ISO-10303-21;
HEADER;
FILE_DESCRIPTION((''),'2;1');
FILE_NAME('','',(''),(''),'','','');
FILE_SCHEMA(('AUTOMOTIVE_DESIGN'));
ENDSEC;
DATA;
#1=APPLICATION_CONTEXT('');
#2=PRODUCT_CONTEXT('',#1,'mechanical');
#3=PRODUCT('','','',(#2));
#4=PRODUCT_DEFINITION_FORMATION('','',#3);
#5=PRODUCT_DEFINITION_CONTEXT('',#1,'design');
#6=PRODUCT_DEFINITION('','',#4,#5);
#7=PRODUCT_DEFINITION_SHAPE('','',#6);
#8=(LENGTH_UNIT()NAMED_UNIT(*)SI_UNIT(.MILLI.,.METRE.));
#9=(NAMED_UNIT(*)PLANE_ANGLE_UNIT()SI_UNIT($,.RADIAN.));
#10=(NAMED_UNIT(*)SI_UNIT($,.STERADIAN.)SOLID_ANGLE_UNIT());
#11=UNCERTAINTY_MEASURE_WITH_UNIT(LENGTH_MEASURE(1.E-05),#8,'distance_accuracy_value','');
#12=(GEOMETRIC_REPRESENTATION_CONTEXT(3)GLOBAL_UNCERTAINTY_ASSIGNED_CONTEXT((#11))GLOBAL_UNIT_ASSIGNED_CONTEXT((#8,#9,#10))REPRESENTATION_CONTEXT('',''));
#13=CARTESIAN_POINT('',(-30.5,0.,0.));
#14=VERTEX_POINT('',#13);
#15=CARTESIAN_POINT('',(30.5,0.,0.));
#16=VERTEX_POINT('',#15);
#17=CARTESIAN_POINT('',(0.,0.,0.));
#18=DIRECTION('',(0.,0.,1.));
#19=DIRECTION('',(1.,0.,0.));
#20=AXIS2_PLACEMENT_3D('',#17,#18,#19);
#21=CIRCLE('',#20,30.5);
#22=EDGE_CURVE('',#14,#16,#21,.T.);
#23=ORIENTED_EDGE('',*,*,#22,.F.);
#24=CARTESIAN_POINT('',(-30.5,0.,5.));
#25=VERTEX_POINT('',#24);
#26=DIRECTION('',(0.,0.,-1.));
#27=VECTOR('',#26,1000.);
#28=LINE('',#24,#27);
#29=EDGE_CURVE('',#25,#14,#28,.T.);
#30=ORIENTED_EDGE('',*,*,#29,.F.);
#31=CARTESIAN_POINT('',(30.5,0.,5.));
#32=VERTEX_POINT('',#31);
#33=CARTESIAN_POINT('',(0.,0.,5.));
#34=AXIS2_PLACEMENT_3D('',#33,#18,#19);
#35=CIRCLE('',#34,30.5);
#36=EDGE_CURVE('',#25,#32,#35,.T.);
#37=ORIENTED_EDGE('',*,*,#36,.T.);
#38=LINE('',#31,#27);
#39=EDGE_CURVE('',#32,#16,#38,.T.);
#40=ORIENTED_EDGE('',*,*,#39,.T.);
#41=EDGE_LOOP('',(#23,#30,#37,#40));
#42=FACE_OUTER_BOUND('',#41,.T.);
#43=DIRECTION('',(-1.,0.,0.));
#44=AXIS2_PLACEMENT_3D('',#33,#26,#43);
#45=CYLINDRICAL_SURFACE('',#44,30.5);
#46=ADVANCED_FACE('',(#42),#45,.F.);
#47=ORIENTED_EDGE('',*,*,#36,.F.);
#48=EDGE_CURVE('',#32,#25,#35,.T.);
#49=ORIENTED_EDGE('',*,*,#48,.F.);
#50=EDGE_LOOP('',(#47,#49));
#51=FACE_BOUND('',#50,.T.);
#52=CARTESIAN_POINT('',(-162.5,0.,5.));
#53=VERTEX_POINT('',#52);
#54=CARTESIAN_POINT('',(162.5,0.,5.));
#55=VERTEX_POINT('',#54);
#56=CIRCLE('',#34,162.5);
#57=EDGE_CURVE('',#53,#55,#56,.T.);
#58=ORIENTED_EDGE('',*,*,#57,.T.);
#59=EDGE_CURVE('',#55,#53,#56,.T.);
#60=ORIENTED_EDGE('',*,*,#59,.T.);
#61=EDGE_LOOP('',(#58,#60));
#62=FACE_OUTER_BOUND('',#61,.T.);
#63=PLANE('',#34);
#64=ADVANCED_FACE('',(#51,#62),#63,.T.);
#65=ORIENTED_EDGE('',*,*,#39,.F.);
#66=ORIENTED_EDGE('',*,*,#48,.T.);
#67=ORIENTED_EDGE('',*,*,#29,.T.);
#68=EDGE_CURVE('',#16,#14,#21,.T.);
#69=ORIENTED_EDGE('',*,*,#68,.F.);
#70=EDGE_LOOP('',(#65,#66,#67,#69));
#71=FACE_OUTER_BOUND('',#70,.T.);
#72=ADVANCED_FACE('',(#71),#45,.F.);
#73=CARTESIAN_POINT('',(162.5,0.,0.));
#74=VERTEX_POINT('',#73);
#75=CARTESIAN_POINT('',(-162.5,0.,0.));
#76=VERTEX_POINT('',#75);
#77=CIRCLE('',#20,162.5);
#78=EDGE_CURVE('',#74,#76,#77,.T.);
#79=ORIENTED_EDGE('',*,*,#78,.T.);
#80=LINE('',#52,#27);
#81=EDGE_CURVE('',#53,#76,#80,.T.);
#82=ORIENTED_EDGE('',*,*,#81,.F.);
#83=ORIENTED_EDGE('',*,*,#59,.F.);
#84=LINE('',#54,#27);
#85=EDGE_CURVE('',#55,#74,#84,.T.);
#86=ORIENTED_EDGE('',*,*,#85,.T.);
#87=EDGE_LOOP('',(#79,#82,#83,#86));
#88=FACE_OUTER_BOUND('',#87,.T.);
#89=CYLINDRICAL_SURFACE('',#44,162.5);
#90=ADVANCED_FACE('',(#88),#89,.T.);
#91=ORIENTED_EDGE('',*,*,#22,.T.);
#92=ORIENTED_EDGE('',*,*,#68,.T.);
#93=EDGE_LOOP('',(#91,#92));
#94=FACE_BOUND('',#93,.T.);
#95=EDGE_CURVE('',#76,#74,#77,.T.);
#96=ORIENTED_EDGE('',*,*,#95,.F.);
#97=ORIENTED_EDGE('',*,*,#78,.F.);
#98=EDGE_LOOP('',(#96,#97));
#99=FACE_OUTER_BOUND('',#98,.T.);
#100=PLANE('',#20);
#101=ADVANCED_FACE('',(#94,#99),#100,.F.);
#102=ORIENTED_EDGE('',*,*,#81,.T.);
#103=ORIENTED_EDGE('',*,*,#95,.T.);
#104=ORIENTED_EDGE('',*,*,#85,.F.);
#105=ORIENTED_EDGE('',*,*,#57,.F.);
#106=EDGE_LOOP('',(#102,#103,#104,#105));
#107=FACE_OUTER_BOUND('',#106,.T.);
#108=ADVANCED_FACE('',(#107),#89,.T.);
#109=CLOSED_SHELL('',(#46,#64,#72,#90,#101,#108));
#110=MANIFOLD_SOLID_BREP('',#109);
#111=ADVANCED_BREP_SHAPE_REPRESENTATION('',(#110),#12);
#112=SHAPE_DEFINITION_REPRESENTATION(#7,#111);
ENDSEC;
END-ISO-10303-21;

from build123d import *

# Parameters (mm, degrees)
SKETCH1_R           = 162.5
SKETCH1_R_2         = 30.5
BOSS_EXTRUDE1_DEPTH = 5


with BuildPart() as part:
    # Sketch1 → Boss-Extrude1 (new body)
    with BuildSketch(Plane.XY):
        Circle(SKETCH1_R)
        Circle(SKETCH1_R_2, mode=Mode.SUBTRACT)
    extrude(amount=BOSS_EXTRUDE1_DEPTH)


solid = part.part
